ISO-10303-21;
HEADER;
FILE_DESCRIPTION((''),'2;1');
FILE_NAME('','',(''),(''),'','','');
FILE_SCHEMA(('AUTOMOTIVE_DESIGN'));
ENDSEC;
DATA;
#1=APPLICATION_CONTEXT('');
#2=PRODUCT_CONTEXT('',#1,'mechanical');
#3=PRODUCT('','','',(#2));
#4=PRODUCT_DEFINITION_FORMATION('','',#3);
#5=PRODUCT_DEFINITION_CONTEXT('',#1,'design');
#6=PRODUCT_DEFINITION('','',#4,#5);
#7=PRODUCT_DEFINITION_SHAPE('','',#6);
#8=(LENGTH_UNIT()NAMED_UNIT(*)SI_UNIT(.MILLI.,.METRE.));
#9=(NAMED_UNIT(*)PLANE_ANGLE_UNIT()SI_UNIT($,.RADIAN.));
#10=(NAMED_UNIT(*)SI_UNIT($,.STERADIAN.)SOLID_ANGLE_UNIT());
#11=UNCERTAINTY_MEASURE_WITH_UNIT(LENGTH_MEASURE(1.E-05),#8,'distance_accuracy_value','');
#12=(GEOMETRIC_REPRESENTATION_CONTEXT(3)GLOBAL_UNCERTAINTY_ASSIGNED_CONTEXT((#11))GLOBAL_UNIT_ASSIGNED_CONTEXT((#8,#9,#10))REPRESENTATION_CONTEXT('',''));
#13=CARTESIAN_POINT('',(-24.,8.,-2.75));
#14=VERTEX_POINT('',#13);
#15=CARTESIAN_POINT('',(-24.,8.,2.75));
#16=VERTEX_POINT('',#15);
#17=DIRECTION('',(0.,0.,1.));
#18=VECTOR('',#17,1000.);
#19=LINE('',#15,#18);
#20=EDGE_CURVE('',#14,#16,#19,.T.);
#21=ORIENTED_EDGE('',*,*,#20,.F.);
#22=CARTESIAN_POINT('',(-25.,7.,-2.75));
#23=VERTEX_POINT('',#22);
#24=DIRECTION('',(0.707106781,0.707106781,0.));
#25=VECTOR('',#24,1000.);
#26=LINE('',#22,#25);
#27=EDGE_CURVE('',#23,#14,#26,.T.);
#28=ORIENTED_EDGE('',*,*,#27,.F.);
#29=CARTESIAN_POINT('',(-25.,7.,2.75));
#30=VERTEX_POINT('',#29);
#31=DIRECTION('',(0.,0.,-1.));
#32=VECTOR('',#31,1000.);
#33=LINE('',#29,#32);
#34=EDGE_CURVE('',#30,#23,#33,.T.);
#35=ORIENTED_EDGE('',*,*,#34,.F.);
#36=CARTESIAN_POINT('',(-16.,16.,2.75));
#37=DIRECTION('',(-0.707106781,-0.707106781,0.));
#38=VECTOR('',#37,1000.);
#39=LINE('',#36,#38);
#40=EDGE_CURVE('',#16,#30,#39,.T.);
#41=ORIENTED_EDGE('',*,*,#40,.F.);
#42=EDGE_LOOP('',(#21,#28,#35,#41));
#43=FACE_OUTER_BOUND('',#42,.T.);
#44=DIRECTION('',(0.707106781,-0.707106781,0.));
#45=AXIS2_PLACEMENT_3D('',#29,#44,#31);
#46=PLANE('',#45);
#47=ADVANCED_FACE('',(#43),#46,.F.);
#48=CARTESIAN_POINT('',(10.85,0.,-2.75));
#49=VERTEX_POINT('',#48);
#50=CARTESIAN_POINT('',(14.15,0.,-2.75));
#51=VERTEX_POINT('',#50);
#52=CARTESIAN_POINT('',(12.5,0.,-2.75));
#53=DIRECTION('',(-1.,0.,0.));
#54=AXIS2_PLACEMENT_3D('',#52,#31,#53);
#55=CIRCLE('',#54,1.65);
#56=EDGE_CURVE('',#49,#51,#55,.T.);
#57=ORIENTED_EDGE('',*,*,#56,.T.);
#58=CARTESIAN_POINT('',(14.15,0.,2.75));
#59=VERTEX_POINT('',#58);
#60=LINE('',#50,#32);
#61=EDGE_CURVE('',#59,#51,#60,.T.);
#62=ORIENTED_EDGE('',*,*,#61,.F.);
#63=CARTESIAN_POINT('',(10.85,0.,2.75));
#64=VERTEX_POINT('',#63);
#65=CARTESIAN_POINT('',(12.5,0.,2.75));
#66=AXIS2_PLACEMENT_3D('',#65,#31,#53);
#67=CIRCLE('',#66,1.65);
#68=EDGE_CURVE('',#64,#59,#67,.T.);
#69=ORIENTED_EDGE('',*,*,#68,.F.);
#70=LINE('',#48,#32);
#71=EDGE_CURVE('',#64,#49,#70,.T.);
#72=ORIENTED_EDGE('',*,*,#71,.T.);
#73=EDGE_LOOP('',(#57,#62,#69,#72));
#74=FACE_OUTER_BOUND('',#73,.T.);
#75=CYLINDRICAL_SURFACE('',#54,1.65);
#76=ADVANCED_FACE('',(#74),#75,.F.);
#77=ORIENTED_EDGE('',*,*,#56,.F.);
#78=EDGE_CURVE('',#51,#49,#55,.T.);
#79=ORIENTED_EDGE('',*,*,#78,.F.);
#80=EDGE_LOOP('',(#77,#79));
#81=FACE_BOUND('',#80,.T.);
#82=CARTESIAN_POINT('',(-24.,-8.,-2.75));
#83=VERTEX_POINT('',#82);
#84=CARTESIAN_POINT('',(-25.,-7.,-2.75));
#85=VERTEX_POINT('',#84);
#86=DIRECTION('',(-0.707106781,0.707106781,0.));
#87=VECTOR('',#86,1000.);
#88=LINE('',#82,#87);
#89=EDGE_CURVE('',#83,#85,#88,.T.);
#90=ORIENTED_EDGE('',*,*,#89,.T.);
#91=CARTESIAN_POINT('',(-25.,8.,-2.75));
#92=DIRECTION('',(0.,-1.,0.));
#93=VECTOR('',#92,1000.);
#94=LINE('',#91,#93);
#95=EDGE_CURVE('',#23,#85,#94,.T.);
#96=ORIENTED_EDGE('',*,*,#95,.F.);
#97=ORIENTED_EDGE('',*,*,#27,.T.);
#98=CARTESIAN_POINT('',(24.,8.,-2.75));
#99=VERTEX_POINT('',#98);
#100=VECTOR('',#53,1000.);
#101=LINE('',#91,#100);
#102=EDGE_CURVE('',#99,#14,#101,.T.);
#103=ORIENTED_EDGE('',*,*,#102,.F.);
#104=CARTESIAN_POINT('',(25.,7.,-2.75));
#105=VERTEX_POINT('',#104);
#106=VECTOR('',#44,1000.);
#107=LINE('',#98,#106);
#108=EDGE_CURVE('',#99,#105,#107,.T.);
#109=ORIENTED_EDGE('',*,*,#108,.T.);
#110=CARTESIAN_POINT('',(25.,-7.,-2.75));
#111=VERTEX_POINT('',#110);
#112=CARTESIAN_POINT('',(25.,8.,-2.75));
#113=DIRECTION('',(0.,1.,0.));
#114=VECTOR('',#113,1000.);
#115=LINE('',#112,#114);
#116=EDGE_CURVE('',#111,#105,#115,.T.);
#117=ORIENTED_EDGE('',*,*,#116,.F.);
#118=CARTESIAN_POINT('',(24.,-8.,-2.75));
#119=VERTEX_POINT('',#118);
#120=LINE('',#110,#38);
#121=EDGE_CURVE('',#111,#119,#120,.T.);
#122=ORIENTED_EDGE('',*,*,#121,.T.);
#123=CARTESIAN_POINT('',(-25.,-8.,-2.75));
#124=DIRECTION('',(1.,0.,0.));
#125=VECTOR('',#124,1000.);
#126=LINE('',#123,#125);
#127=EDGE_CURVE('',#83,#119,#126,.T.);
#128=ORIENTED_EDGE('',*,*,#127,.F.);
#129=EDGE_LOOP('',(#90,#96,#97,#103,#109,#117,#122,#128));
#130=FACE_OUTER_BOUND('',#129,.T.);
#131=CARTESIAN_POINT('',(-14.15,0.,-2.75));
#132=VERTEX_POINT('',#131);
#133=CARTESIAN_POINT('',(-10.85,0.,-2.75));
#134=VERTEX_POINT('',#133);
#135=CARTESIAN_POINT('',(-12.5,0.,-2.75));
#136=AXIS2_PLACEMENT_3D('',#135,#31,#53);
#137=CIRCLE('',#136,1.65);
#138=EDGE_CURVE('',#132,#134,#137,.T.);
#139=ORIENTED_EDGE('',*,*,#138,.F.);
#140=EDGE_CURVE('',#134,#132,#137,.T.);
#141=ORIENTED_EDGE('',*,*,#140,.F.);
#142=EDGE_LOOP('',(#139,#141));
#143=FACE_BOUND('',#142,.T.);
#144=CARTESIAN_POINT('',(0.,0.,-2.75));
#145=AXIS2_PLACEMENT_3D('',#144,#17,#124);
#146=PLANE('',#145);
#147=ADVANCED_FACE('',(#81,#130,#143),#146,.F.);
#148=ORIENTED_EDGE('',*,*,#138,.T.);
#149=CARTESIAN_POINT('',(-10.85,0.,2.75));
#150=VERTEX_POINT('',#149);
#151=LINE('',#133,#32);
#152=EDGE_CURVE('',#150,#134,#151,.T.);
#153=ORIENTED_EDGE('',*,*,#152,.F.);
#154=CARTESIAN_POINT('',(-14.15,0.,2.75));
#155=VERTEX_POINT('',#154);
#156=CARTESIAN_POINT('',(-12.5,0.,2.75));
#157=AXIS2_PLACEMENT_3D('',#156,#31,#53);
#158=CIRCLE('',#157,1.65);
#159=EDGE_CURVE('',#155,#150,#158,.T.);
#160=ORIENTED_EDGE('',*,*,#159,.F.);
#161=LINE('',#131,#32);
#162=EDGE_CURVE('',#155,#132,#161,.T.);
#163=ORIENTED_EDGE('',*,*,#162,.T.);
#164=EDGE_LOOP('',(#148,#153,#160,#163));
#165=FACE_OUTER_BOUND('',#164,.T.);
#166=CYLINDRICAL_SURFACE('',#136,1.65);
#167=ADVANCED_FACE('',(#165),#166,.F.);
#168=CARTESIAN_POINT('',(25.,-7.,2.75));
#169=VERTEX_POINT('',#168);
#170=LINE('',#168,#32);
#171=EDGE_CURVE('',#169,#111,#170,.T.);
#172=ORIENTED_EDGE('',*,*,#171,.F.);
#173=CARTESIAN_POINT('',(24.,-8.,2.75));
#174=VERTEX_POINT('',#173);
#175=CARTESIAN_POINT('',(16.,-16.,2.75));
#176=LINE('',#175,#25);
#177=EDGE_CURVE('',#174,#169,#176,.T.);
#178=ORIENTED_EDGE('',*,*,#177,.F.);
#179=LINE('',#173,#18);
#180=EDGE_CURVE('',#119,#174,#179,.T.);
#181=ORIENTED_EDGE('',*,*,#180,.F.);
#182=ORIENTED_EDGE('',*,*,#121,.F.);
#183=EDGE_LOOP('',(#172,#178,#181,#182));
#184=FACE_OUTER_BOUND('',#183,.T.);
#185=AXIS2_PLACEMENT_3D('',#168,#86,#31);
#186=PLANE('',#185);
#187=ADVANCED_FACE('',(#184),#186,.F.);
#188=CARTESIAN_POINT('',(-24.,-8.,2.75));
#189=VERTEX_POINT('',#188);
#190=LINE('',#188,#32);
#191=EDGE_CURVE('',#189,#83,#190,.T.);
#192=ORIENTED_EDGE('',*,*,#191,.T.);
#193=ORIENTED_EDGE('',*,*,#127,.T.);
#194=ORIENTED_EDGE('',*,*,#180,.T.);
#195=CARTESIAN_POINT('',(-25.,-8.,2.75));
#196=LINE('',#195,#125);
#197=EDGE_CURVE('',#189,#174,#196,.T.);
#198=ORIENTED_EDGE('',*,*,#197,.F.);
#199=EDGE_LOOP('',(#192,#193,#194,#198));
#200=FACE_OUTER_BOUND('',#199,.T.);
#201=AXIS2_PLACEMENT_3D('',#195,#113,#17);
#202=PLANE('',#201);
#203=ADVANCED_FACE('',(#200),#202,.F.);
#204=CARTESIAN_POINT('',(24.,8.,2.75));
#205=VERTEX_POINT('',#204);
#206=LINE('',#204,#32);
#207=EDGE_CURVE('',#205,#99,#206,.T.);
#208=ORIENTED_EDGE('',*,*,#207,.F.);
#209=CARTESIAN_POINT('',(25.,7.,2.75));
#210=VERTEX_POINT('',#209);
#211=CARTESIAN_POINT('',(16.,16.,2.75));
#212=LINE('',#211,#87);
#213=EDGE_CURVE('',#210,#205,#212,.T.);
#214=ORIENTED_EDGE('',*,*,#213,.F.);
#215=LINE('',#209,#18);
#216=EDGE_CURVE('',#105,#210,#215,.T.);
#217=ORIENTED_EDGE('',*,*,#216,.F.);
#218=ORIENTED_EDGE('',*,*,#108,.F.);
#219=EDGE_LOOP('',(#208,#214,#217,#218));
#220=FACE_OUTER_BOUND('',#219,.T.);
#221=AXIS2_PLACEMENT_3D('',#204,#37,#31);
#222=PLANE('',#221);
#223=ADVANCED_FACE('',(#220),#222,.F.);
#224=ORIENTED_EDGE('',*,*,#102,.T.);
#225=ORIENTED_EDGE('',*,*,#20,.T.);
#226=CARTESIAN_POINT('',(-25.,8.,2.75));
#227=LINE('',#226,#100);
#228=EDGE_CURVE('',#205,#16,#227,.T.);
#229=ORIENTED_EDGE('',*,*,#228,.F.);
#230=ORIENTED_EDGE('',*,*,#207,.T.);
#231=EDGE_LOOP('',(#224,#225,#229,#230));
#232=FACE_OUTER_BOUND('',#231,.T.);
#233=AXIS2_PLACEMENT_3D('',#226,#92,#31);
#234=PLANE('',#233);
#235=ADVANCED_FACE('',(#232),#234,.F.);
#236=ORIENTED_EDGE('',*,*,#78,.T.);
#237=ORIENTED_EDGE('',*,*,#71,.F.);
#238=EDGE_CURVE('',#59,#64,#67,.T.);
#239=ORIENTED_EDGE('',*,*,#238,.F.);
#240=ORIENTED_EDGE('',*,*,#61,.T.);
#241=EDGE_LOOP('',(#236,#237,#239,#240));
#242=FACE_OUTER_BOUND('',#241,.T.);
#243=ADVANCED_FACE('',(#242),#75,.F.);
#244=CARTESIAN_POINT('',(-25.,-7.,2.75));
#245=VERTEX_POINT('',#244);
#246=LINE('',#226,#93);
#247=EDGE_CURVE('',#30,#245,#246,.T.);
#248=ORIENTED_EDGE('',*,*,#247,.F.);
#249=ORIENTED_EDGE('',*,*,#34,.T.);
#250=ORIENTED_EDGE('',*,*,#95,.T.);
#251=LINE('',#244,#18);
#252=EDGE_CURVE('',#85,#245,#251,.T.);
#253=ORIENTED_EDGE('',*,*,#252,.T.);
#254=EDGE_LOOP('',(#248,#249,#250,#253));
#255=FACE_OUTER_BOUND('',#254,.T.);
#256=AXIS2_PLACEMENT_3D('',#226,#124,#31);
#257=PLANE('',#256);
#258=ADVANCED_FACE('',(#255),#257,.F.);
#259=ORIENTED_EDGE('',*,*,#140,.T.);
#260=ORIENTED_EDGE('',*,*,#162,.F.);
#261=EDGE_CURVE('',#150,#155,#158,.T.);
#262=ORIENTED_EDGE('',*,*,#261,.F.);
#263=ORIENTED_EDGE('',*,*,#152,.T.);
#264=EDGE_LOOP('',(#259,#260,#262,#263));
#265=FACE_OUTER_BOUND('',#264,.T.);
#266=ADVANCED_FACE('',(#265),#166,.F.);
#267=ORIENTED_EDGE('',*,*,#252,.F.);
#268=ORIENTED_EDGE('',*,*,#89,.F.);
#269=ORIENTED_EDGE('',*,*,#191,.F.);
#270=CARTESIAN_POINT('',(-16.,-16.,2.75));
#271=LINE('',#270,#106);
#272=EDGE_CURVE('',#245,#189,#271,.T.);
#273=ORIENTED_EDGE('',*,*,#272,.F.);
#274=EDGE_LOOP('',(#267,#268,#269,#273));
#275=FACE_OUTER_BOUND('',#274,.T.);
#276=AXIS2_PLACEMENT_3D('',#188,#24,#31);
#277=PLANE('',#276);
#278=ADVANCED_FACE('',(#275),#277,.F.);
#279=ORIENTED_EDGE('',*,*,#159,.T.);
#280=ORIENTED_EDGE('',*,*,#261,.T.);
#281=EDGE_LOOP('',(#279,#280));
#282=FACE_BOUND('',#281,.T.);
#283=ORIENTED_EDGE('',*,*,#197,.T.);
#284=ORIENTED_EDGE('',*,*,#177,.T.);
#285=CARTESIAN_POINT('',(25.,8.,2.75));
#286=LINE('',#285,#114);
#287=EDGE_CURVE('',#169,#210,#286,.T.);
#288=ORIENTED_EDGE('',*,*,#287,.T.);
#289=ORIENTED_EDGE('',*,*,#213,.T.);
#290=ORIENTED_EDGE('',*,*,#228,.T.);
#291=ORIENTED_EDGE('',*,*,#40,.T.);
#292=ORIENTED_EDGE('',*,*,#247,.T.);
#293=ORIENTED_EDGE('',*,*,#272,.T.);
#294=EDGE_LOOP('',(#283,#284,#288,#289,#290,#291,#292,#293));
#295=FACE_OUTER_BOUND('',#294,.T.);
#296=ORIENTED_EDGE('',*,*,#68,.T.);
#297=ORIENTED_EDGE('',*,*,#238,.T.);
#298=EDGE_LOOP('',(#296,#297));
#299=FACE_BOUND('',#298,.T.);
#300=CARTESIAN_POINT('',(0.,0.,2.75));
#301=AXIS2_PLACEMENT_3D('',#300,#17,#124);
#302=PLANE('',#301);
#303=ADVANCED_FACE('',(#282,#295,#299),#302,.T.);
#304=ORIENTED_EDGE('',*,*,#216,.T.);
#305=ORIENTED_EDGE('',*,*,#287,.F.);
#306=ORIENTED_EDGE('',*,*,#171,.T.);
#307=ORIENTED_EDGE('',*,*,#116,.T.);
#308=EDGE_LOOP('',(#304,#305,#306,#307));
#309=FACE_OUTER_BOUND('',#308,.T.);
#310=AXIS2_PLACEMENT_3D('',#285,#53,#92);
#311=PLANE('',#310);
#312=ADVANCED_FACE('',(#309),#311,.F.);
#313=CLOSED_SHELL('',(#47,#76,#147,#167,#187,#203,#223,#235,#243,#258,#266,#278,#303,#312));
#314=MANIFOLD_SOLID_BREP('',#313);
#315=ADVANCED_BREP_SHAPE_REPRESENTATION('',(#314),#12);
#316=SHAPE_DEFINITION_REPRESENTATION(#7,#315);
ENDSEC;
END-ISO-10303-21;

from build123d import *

# Parameters (mm, degrees)
SKETCH_1_W         = 50
SKETCH_1_H         = 16
EXTRUDE_1_DEPTH    = 2.75
HOLE_WIZARD_M4_1_D = 3.3
CHAMFER_1_SIZE     = 1


with BuildPart() as part:
    # 草图1 → 凸台-拉伸1 (new, symmetric)
    with BuildSketch(Plane.XY):
        Rectangle(SKETCH_1_W, SKETCH_1_H)
    extrude(amount=EXTRUDE_1_DEPTH, both=True)

    # M4 螺纹孔1 (through all)
    with Locations(Plane(origin=(0, 0, -2.75), x_dir=(-1, 0, 0), z_dir=(0, 0, -1))):
        with Locations((12.5, 0), (-12.5, 0)):
            Hole(HOLE_WIZARD_M4_1_D / 2)

    # 倒角1
    chamfer_1_edges = [part.edges().sort_by_distance(p)[0] for p in [
        (25, -8, 0),
        (-25, -8, 0),
        (-25, 8, 0),
        (25, 8, 0),
    ]]
    chamfer(chamfer_1_edges, length=CHAMFER_1_SIZE)


solid = part.part
